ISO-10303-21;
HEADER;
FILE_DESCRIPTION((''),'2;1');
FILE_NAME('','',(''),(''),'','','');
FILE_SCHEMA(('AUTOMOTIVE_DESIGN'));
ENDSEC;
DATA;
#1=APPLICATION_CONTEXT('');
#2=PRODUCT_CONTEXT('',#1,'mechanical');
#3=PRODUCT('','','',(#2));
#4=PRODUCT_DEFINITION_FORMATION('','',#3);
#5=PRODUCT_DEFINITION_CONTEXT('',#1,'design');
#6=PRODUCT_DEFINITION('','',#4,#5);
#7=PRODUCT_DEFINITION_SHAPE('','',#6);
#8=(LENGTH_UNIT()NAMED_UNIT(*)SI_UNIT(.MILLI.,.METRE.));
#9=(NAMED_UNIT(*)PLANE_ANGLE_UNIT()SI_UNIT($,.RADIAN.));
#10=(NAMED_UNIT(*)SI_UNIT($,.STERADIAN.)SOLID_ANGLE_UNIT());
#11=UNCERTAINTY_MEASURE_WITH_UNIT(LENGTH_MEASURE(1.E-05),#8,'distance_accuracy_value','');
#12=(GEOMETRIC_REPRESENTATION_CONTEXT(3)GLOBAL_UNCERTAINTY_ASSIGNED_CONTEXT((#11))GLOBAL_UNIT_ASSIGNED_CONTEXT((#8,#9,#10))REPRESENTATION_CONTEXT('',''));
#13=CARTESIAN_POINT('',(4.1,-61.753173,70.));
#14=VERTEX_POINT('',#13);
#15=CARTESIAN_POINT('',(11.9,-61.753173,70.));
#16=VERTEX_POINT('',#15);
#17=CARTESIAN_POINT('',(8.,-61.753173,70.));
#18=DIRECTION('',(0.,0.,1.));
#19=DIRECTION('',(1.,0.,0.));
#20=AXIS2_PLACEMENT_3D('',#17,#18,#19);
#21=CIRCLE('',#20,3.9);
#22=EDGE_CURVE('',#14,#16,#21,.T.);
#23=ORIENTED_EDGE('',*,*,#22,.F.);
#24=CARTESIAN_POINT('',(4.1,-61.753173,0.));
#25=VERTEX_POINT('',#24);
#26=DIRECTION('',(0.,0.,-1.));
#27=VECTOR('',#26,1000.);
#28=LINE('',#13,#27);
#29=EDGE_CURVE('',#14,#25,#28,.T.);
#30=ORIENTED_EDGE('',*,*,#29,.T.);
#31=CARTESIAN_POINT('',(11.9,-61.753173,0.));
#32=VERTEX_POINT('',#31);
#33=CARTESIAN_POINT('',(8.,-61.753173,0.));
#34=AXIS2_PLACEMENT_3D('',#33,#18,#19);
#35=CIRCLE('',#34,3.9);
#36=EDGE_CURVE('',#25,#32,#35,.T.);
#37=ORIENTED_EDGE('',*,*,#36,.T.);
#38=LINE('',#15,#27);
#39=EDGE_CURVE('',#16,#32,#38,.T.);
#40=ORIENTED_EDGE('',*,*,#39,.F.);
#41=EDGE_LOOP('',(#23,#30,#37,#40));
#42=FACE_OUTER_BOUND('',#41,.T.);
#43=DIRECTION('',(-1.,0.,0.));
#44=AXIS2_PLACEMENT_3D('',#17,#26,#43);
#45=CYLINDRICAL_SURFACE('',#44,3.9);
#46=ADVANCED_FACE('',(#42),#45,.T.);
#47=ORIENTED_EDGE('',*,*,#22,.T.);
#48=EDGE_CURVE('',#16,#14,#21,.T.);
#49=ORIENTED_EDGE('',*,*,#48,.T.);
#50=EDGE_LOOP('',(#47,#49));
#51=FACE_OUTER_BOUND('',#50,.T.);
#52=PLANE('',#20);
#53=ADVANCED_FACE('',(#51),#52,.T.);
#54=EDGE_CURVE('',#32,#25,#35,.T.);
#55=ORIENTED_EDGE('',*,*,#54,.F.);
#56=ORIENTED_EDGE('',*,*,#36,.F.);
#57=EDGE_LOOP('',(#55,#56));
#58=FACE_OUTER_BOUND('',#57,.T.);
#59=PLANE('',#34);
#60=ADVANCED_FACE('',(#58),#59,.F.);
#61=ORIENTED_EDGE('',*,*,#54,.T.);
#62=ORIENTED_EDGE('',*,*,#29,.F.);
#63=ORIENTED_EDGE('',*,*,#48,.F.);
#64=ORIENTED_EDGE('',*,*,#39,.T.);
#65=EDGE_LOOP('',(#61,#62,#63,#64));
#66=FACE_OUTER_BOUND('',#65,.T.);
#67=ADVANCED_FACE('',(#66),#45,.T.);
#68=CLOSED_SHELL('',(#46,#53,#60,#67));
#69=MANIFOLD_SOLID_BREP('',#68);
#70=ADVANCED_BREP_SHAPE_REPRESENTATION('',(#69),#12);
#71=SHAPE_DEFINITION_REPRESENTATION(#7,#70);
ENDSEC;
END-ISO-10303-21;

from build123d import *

# Parameters (mm, degrees)
SKETCH1_R           = 3.9
BOSS_EXTRUDE1_DEPTH = 70


with BuildPart() as part:
    # Sketch1 → Boss-Extrude1 (new body)
    with BuildSketch(Plane.XY):
        with Locations((8, -61.753173354)):
            Circle(SKETCH1_R)
    extrude(amount=BOSS_EXTRUDE1_DEPTH)


solid = part.part
